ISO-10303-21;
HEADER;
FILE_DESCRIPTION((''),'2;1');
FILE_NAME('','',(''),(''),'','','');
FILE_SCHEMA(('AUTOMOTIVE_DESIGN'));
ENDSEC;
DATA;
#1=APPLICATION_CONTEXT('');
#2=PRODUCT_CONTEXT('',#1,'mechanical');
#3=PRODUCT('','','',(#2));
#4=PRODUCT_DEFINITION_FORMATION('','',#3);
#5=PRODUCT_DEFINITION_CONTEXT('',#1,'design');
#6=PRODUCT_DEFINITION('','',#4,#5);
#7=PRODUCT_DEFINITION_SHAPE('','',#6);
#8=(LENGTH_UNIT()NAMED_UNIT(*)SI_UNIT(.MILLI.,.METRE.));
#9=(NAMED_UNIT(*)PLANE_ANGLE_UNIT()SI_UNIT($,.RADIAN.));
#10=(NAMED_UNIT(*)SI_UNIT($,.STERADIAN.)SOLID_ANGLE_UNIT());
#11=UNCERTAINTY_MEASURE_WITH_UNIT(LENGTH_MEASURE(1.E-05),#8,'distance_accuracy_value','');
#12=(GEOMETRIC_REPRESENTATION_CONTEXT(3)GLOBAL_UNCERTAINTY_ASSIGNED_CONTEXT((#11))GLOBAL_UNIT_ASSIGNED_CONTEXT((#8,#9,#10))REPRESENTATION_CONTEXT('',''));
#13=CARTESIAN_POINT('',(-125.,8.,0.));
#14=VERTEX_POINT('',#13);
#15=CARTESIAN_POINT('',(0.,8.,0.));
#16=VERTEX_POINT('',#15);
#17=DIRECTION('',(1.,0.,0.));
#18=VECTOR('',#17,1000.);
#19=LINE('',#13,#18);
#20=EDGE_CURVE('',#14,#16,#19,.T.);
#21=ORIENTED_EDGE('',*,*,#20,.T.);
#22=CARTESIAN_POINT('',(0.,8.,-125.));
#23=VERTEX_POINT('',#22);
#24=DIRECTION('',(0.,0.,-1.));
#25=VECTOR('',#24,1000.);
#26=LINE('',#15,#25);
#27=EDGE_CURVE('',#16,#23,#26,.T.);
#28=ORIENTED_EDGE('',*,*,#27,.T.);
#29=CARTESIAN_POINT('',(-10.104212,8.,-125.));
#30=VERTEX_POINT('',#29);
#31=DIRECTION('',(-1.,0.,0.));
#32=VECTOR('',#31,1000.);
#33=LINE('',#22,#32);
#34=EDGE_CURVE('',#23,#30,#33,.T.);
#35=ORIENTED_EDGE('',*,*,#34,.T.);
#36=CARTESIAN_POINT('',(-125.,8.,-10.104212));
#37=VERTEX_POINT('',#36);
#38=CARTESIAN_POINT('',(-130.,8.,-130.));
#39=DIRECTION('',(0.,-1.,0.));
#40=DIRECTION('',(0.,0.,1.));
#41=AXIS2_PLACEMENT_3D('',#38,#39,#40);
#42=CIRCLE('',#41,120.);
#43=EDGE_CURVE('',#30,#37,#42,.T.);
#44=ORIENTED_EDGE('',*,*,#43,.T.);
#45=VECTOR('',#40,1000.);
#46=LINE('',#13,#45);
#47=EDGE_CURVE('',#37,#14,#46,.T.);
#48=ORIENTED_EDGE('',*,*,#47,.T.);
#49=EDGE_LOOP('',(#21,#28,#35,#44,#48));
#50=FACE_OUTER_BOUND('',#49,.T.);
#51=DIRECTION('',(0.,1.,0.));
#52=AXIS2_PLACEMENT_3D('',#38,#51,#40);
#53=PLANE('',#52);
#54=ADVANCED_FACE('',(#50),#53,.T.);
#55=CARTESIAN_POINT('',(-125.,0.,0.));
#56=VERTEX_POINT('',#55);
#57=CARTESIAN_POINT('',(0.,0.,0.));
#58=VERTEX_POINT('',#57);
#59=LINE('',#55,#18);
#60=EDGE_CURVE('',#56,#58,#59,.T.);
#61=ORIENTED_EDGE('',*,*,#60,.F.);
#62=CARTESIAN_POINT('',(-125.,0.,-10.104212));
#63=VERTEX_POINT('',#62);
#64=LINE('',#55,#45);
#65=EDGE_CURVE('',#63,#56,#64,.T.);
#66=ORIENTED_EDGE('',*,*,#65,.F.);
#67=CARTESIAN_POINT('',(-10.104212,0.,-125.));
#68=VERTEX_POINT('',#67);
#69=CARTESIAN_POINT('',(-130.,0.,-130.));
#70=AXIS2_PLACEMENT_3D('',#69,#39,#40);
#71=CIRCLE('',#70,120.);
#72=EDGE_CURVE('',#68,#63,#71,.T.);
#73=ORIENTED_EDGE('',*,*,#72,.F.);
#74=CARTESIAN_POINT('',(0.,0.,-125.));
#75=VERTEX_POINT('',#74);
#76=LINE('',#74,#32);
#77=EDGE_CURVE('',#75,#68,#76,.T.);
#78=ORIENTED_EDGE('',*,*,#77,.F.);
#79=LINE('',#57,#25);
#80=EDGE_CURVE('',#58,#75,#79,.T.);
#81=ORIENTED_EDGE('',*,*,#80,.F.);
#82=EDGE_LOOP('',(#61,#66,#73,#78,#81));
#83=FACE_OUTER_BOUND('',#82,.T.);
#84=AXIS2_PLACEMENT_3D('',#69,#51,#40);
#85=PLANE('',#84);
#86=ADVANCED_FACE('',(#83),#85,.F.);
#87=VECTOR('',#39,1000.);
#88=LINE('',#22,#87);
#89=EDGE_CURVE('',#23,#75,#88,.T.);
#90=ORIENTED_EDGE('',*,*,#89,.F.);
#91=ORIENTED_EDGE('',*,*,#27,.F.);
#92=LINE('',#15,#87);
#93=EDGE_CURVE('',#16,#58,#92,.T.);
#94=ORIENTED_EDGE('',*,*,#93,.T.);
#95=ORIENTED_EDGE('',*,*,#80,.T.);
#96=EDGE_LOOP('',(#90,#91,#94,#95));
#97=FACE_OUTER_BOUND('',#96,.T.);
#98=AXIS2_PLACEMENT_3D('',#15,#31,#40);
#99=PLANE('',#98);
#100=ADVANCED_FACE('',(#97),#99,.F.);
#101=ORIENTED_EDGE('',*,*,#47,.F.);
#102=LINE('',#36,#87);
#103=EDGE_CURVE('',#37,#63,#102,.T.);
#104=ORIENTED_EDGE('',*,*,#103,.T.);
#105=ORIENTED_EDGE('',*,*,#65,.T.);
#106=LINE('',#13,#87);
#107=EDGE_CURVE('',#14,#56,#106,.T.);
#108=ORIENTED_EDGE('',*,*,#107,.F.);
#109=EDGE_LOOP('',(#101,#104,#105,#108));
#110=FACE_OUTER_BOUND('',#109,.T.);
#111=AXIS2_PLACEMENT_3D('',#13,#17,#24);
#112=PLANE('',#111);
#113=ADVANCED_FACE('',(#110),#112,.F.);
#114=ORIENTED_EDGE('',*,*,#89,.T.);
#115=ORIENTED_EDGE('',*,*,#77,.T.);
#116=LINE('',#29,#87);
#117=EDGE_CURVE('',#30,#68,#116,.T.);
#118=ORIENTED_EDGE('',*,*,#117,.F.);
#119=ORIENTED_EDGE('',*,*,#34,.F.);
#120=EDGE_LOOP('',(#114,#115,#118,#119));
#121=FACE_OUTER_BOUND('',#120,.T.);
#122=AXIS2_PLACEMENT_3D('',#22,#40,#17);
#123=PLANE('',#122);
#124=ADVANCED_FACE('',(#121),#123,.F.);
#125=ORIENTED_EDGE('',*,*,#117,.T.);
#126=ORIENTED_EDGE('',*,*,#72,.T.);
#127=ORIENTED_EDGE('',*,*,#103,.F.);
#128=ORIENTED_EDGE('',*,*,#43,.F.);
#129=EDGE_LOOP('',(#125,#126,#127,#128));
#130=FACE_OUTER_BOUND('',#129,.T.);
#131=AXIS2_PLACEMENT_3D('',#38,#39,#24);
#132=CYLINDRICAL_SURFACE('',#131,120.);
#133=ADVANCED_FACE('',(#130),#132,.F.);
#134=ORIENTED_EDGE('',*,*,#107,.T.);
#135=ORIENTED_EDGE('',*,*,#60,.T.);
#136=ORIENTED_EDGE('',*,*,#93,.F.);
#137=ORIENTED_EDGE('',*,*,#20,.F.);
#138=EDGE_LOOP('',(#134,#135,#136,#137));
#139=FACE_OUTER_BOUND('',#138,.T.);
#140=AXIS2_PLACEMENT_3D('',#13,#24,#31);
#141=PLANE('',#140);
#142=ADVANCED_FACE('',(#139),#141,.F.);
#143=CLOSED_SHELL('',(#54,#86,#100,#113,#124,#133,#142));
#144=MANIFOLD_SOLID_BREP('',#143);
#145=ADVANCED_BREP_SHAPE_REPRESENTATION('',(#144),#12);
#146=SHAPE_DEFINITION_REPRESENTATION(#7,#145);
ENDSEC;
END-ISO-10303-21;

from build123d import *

# Parameters (mm, degrees)
EXTRUDE_1_DEPTH = 8


with BuildPart() as part:
    # 草图1 → 凸台-拉伸1 (new body)
    with BuildSketch(Plane(origin=(0, 0, 0), x_dir=(1, 0, 0), z_dir=(0, 1, 0))):
        with BuildLine():
            Line((-125, 0), (0, 0))
            Line((0, 0), (0, 125))
            Line((0, 125), (-10.104211917, 125))
            ThreePointArc((-10.104211917, 125), (-45.147186258, 45.147186258), (-125, 10.104211917))
            Line((-125, 10.104211917), (-125, 0))
        make_face()
    extrude(amount=EXTRUDE_1_DEPTH)


solid = part.part
